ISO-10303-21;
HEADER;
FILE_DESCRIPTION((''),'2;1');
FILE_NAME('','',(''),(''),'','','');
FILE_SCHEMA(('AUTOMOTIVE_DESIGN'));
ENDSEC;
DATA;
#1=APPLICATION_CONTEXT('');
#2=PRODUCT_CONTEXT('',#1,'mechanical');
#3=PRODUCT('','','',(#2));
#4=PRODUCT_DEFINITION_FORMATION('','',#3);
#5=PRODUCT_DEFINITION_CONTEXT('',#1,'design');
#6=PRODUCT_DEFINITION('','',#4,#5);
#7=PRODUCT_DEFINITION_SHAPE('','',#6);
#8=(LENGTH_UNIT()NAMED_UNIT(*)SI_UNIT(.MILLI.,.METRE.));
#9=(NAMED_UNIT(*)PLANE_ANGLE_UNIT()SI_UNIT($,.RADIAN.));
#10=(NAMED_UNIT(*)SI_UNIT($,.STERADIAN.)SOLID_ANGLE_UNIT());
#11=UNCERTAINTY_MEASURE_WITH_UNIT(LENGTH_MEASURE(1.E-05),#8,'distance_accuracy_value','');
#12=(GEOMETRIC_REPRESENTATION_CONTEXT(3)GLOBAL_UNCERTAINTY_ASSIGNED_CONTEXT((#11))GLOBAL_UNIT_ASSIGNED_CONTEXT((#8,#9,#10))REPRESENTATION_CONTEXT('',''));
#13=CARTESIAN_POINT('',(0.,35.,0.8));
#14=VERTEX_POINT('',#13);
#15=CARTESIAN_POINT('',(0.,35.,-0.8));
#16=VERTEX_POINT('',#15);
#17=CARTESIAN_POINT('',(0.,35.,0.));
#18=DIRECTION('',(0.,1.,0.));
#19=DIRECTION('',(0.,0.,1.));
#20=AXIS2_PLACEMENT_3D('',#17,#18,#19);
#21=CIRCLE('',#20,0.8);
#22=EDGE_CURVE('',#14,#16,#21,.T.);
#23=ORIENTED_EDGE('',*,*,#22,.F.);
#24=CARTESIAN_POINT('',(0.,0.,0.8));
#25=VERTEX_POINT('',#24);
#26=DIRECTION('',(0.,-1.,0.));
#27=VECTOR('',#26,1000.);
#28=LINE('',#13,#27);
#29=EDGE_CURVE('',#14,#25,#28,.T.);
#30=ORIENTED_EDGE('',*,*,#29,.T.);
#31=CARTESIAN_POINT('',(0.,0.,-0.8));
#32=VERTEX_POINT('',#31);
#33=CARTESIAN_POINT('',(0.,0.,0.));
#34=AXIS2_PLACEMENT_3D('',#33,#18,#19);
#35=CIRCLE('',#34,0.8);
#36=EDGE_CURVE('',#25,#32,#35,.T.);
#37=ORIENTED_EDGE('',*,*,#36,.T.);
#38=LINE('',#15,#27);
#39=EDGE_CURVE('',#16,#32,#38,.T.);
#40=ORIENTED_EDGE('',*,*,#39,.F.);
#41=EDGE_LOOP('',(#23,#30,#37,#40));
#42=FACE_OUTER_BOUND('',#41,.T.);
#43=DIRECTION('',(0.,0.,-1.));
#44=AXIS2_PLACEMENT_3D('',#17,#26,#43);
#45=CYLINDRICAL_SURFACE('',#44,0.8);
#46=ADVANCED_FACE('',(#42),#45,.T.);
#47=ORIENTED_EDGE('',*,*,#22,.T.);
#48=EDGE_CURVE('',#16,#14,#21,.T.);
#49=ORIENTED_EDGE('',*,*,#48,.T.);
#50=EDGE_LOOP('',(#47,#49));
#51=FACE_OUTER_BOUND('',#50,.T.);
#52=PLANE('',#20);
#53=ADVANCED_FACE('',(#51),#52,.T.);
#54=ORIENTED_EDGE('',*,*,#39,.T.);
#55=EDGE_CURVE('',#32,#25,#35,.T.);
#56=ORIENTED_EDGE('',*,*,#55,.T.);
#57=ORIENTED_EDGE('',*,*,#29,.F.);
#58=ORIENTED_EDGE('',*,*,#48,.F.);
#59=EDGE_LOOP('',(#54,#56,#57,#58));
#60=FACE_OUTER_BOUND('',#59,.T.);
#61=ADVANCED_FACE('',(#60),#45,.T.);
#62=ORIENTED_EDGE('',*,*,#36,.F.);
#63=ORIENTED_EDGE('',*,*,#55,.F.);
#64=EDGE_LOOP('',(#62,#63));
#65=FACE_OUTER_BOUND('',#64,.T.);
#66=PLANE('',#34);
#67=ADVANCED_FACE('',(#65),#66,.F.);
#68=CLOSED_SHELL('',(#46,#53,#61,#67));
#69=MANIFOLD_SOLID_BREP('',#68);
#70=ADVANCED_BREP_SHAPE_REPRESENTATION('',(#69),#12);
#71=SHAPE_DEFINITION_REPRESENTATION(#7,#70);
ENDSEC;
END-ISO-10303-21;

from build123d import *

# Parameters (mm, degrees)
SKETCH1_R           = 0.8
BOSS_EXTRUDE1_DEPTH = 35


with BuildPart() as part:
    # Sketch1 → Boss-Extrude1 (new body)
    with BuildSketch(Plane(origin=(0, 0, 0), x_dir=(1, 0, 0), z_dir=(0, 1, 0))):
        with Locations(Location((0, 0, 0), (0, 0, 270))):
            Circle(SKETCH1_R)
    extrude(amount=BOSS_EXTRUDE1_DEPTH)


solid = part.part
